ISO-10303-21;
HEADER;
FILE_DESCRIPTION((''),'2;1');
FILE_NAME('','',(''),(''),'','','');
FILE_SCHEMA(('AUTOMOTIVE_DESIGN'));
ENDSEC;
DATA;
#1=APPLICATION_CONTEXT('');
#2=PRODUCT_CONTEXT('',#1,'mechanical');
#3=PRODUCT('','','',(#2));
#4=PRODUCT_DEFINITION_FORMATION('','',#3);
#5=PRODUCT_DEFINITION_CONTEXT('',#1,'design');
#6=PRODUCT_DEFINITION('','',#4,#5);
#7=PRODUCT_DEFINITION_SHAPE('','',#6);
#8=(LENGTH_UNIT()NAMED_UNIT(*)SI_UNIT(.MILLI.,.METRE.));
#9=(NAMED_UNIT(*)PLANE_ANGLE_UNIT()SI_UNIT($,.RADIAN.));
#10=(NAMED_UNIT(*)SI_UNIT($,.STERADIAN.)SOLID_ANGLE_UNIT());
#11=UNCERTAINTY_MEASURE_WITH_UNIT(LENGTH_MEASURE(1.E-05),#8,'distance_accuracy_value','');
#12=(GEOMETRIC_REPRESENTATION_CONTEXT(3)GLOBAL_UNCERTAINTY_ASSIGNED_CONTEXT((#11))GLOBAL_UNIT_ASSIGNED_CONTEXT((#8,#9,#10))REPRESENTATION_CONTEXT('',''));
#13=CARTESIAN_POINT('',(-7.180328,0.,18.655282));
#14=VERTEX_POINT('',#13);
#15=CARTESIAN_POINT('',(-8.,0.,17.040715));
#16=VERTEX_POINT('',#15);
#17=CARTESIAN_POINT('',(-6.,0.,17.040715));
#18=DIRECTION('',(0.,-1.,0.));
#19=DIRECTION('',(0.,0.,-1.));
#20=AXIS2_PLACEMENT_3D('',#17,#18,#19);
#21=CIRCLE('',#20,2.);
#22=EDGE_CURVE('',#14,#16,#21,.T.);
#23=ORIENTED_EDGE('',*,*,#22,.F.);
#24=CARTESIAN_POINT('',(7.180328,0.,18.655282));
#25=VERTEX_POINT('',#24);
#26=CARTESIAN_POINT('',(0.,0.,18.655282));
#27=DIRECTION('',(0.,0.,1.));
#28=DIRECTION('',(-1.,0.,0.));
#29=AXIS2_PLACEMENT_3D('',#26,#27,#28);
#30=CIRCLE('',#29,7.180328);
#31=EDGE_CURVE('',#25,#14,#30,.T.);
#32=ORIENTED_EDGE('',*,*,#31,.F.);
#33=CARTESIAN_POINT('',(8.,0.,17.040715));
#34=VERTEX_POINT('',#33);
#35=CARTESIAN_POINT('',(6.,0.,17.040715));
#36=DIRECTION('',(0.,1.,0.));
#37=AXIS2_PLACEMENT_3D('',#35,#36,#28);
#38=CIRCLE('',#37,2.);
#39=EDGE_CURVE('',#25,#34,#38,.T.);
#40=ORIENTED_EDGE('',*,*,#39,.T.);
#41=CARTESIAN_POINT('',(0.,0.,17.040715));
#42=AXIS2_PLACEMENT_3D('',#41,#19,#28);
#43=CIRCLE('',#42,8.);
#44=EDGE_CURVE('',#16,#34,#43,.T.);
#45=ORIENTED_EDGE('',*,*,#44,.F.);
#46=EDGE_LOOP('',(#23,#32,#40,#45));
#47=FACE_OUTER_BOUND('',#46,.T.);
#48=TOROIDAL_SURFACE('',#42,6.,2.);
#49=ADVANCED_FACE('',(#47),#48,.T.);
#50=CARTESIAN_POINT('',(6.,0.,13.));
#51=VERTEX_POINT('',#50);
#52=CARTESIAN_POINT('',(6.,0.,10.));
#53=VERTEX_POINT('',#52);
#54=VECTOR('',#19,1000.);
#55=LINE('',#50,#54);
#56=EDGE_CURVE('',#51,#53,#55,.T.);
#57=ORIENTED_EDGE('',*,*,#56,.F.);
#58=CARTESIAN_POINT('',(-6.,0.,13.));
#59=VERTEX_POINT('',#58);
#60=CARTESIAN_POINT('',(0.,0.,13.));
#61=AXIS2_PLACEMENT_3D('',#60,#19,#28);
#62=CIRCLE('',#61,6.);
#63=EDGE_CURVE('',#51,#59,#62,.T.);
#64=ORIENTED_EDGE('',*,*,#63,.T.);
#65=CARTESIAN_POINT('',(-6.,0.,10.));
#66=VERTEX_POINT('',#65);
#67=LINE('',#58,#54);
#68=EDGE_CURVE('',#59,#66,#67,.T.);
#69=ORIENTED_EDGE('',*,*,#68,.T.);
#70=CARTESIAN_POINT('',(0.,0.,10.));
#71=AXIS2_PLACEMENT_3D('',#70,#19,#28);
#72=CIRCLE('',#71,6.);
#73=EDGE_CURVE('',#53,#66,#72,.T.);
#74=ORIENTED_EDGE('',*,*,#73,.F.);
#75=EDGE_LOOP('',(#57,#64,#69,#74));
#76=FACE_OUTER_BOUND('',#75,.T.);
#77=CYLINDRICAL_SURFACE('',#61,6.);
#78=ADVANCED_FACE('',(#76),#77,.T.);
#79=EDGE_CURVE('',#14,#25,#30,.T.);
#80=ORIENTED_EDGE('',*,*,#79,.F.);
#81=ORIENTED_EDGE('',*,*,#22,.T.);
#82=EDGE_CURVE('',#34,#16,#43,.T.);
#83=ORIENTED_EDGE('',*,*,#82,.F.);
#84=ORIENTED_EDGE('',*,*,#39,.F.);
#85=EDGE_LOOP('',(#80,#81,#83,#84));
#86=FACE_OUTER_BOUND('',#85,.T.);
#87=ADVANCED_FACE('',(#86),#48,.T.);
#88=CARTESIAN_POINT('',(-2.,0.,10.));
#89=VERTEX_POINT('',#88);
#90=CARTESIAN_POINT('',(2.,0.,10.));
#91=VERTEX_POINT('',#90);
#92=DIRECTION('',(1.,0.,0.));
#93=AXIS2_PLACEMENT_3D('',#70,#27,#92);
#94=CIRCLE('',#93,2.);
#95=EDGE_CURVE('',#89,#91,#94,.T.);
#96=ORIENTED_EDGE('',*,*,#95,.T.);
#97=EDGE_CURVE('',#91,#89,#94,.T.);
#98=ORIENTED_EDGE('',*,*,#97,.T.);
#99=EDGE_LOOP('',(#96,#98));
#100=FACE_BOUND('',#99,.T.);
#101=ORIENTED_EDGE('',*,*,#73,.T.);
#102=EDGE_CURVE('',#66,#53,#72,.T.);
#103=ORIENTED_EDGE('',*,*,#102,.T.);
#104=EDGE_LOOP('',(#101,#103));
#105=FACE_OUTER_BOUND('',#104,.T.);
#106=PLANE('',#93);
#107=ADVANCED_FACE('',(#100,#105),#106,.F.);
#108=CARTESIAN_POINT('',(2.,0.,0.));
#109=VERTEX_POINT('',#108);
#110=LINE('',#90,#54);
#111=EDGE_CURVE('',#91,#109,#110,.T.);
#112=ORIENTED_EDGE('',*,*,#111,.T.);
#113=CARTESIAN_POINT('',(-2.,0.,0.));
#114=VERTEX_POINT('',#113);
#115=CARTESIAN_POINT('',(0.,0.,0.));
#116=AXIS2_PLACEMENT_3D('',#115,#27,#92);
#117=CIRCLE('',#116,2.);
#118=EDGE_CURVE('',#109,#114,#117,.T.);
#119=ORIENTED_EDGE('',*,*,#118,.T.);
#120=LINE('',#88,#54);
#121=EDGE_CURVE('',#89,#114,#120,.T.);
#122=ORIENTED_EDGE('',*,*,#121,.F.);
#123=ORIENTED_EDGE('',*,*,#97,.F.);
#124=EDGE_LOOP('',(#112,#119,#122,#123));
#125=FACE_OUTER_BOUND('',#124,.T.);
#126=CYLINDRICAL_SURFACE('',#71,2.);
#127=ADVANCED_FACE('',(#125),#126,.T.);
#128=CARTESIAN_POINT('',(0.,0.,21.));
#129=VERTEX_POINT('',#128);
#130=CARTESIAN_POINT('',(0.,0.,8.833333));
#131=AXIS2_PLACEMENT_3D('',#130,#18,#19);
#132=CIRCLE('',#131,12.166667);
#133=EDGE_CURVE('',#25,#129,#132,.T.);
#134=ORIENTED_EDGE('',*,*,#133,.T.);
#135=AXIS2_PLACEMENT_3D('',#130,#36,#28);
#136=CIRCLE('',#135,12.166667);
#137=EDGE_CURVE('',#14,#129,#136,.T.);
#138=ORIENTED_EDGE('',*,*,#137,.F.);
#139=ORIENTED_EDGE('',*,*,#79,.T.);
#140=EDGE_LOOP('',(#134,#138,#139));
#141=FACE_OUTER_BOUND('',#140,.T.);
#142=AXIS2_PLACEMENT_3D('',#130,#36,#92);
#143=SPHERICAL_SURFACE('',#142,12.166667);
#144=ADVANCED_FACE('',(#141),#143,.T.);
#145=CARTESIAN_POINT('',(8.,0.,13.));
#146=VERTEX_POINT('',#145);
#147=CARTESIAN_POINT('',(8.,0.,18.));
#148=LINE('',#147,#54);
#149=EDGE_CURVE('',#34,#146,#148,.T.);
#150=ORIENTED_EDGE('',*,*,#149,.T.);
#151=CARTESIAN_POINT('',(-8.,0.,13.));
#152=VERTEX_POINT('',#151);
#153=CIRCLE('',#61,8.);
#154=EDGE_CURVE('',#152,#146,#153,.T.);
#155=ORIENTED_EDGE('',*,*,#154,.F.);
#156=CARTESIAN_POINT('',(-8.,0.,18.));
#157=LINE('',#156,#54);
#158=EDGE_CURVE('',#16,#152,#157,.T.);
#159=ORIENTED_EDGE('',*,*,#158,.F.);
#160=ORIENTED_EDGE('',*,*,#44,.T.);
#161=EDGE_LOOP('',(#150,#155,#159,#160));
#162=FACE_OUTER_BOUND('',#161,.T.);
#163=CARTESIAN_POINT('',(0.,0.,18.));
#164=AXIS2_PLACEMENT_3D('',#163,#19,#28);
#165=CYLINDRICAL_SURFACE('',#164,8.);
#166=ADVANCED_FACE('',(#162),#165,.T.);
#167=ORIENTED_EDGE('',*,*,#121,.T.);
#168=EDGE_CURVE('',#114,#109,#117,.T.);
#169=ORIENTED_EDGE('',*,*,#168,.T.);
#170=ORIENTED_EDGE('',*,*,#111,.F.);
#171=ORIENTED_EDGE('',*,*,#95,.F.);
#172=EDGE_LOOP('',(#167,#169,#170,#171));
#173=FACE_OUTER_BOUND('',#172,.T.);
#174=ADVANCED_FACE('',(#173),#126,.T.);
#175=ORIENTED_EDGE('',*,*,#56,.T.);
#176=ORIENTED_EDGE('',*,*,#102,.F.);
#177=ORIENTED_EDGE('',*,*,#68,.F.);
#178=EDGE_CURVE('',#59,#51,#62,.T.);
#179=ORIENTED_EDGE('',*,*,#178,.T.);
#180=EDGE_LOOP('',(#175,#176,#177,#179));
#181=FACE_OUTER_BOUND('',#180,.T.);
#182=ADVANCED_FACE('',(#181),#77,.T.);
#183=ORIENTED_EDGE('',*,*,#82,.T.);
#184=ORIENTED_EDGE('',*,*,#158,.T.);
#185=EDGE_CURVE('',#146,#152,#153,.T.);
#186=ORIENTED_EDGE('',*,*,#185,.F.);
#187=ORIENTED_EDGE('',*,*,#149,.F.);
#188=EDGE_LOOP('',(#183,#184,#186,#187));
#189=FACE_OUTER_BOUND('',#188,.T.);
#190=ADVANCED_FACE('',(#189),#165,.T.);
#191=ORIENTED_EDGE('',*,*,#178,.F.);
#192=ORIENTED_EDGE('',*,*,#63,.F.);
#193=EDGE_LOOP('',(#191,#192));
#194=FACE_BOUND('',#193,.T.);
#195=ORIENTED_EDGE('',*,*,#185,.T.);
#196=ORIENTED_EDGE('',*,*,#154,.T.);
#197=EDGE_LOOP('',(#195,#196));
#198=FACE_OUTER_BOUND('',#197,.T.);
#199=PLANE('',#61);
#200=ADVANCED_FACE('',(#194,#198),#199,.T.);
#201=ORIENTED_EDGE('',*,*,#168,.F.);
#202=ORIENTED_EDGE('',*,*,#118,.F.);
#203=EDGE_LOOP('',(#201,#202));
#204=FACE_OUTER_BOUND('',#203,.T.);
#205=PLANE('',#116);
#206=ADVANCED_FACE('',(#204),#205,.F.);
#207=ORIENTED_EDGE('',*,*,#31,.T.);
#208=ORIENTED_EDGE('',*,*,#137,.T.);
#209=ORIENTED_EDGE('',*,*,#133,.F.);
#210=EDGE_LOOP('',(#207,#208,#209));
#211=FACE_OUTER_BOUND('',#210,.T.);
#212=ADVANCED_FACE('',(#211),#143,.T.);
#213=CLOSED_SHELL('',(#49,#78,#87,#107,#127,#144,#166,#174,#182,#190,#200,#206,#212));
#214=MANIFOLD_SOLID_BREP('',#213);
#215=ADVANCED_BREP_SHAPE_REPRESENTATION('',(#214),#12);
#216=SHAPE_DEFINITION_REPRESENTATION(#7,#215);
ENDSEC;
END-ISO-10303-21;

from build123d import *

# Parameters (mm, degrees)
SKETCH1_R           = 2
BOSS_EXTRUDE1_DEPTH = 10
SKETCH2_R           = 8
BOSS_EXTRUDE2_DEPTH = 8
SKETCH3_R           = 8
SKETCH3_R_2         = 6
CUT_EXTRUDE1_DEPTH  = 3
DOME1_FACE_RADIUS   = 8
DOME1_HEIGHT        = 3
FILLET1_R           = 2


with BuildPart() as part:
    # Sketch1 → Boss-Extrude1 (new body)
    with BuildSketch(Plane.XY):
        Circle(SKETCH1_R)
    extrude(amount=BOSS_EXTRUDE1_DEPTH)

    # Sketch2 → Boss-Extrude2 (add)
    with BuildSketch(Plane.XY.offset(10)):
        Circle(SKETCH2_R)
    extrude(amount=BOSS_EXTRUDE2_DEPTH)

    # Sketch3 → Cut-Extrude1 (cut)
    with BuildSketch(Plane(origin=(0, 0, 10), x_dir=(-1, 0, 0), z_dir=(0, 0, -1))):
        Circle(SKETCH3_R)
        Circle(SKETCH3_R_2, mode=Mode.SUBTRACT)
    extrude(amount=-CUT_EXTRUDE1_DEPTH, mode=Mode.SUBTRACT)

    # Dome1: a dome of height H over a round flat face of radius A is a cap of a sphere of radius (A * A + H * H) / (2 * H)
    dome1_r = (DOME1_FACE_RADIUS * DOME1_FACE_RADIUS + DOME1_HEIGHT * DOME1_HEIGHT) / (2 * DOME1_HEIGHT)
    dome1_base = Plane((0, 0, 18), z_dir=(0, 0, 1))
    with Locations(dome1_base.offset(DOME1_HEIGHT - dome1_r)):
        dome1_ball = Sphere(dome1_r, mode=Mode.PRIVATE)
    add(split(dome1_ball, bisect_by=dome1_base, keep=Keep.TOP, mode=Mode.PRIVATE))

    # Fillet1
    fillet1_edges = [part.edges().sort_by_distance(p)[0] for p in [
        (-8, 0, 18),
    ]]
    fillet(fillet1_edges, radius=FILLET1_R)


solid = part.part
